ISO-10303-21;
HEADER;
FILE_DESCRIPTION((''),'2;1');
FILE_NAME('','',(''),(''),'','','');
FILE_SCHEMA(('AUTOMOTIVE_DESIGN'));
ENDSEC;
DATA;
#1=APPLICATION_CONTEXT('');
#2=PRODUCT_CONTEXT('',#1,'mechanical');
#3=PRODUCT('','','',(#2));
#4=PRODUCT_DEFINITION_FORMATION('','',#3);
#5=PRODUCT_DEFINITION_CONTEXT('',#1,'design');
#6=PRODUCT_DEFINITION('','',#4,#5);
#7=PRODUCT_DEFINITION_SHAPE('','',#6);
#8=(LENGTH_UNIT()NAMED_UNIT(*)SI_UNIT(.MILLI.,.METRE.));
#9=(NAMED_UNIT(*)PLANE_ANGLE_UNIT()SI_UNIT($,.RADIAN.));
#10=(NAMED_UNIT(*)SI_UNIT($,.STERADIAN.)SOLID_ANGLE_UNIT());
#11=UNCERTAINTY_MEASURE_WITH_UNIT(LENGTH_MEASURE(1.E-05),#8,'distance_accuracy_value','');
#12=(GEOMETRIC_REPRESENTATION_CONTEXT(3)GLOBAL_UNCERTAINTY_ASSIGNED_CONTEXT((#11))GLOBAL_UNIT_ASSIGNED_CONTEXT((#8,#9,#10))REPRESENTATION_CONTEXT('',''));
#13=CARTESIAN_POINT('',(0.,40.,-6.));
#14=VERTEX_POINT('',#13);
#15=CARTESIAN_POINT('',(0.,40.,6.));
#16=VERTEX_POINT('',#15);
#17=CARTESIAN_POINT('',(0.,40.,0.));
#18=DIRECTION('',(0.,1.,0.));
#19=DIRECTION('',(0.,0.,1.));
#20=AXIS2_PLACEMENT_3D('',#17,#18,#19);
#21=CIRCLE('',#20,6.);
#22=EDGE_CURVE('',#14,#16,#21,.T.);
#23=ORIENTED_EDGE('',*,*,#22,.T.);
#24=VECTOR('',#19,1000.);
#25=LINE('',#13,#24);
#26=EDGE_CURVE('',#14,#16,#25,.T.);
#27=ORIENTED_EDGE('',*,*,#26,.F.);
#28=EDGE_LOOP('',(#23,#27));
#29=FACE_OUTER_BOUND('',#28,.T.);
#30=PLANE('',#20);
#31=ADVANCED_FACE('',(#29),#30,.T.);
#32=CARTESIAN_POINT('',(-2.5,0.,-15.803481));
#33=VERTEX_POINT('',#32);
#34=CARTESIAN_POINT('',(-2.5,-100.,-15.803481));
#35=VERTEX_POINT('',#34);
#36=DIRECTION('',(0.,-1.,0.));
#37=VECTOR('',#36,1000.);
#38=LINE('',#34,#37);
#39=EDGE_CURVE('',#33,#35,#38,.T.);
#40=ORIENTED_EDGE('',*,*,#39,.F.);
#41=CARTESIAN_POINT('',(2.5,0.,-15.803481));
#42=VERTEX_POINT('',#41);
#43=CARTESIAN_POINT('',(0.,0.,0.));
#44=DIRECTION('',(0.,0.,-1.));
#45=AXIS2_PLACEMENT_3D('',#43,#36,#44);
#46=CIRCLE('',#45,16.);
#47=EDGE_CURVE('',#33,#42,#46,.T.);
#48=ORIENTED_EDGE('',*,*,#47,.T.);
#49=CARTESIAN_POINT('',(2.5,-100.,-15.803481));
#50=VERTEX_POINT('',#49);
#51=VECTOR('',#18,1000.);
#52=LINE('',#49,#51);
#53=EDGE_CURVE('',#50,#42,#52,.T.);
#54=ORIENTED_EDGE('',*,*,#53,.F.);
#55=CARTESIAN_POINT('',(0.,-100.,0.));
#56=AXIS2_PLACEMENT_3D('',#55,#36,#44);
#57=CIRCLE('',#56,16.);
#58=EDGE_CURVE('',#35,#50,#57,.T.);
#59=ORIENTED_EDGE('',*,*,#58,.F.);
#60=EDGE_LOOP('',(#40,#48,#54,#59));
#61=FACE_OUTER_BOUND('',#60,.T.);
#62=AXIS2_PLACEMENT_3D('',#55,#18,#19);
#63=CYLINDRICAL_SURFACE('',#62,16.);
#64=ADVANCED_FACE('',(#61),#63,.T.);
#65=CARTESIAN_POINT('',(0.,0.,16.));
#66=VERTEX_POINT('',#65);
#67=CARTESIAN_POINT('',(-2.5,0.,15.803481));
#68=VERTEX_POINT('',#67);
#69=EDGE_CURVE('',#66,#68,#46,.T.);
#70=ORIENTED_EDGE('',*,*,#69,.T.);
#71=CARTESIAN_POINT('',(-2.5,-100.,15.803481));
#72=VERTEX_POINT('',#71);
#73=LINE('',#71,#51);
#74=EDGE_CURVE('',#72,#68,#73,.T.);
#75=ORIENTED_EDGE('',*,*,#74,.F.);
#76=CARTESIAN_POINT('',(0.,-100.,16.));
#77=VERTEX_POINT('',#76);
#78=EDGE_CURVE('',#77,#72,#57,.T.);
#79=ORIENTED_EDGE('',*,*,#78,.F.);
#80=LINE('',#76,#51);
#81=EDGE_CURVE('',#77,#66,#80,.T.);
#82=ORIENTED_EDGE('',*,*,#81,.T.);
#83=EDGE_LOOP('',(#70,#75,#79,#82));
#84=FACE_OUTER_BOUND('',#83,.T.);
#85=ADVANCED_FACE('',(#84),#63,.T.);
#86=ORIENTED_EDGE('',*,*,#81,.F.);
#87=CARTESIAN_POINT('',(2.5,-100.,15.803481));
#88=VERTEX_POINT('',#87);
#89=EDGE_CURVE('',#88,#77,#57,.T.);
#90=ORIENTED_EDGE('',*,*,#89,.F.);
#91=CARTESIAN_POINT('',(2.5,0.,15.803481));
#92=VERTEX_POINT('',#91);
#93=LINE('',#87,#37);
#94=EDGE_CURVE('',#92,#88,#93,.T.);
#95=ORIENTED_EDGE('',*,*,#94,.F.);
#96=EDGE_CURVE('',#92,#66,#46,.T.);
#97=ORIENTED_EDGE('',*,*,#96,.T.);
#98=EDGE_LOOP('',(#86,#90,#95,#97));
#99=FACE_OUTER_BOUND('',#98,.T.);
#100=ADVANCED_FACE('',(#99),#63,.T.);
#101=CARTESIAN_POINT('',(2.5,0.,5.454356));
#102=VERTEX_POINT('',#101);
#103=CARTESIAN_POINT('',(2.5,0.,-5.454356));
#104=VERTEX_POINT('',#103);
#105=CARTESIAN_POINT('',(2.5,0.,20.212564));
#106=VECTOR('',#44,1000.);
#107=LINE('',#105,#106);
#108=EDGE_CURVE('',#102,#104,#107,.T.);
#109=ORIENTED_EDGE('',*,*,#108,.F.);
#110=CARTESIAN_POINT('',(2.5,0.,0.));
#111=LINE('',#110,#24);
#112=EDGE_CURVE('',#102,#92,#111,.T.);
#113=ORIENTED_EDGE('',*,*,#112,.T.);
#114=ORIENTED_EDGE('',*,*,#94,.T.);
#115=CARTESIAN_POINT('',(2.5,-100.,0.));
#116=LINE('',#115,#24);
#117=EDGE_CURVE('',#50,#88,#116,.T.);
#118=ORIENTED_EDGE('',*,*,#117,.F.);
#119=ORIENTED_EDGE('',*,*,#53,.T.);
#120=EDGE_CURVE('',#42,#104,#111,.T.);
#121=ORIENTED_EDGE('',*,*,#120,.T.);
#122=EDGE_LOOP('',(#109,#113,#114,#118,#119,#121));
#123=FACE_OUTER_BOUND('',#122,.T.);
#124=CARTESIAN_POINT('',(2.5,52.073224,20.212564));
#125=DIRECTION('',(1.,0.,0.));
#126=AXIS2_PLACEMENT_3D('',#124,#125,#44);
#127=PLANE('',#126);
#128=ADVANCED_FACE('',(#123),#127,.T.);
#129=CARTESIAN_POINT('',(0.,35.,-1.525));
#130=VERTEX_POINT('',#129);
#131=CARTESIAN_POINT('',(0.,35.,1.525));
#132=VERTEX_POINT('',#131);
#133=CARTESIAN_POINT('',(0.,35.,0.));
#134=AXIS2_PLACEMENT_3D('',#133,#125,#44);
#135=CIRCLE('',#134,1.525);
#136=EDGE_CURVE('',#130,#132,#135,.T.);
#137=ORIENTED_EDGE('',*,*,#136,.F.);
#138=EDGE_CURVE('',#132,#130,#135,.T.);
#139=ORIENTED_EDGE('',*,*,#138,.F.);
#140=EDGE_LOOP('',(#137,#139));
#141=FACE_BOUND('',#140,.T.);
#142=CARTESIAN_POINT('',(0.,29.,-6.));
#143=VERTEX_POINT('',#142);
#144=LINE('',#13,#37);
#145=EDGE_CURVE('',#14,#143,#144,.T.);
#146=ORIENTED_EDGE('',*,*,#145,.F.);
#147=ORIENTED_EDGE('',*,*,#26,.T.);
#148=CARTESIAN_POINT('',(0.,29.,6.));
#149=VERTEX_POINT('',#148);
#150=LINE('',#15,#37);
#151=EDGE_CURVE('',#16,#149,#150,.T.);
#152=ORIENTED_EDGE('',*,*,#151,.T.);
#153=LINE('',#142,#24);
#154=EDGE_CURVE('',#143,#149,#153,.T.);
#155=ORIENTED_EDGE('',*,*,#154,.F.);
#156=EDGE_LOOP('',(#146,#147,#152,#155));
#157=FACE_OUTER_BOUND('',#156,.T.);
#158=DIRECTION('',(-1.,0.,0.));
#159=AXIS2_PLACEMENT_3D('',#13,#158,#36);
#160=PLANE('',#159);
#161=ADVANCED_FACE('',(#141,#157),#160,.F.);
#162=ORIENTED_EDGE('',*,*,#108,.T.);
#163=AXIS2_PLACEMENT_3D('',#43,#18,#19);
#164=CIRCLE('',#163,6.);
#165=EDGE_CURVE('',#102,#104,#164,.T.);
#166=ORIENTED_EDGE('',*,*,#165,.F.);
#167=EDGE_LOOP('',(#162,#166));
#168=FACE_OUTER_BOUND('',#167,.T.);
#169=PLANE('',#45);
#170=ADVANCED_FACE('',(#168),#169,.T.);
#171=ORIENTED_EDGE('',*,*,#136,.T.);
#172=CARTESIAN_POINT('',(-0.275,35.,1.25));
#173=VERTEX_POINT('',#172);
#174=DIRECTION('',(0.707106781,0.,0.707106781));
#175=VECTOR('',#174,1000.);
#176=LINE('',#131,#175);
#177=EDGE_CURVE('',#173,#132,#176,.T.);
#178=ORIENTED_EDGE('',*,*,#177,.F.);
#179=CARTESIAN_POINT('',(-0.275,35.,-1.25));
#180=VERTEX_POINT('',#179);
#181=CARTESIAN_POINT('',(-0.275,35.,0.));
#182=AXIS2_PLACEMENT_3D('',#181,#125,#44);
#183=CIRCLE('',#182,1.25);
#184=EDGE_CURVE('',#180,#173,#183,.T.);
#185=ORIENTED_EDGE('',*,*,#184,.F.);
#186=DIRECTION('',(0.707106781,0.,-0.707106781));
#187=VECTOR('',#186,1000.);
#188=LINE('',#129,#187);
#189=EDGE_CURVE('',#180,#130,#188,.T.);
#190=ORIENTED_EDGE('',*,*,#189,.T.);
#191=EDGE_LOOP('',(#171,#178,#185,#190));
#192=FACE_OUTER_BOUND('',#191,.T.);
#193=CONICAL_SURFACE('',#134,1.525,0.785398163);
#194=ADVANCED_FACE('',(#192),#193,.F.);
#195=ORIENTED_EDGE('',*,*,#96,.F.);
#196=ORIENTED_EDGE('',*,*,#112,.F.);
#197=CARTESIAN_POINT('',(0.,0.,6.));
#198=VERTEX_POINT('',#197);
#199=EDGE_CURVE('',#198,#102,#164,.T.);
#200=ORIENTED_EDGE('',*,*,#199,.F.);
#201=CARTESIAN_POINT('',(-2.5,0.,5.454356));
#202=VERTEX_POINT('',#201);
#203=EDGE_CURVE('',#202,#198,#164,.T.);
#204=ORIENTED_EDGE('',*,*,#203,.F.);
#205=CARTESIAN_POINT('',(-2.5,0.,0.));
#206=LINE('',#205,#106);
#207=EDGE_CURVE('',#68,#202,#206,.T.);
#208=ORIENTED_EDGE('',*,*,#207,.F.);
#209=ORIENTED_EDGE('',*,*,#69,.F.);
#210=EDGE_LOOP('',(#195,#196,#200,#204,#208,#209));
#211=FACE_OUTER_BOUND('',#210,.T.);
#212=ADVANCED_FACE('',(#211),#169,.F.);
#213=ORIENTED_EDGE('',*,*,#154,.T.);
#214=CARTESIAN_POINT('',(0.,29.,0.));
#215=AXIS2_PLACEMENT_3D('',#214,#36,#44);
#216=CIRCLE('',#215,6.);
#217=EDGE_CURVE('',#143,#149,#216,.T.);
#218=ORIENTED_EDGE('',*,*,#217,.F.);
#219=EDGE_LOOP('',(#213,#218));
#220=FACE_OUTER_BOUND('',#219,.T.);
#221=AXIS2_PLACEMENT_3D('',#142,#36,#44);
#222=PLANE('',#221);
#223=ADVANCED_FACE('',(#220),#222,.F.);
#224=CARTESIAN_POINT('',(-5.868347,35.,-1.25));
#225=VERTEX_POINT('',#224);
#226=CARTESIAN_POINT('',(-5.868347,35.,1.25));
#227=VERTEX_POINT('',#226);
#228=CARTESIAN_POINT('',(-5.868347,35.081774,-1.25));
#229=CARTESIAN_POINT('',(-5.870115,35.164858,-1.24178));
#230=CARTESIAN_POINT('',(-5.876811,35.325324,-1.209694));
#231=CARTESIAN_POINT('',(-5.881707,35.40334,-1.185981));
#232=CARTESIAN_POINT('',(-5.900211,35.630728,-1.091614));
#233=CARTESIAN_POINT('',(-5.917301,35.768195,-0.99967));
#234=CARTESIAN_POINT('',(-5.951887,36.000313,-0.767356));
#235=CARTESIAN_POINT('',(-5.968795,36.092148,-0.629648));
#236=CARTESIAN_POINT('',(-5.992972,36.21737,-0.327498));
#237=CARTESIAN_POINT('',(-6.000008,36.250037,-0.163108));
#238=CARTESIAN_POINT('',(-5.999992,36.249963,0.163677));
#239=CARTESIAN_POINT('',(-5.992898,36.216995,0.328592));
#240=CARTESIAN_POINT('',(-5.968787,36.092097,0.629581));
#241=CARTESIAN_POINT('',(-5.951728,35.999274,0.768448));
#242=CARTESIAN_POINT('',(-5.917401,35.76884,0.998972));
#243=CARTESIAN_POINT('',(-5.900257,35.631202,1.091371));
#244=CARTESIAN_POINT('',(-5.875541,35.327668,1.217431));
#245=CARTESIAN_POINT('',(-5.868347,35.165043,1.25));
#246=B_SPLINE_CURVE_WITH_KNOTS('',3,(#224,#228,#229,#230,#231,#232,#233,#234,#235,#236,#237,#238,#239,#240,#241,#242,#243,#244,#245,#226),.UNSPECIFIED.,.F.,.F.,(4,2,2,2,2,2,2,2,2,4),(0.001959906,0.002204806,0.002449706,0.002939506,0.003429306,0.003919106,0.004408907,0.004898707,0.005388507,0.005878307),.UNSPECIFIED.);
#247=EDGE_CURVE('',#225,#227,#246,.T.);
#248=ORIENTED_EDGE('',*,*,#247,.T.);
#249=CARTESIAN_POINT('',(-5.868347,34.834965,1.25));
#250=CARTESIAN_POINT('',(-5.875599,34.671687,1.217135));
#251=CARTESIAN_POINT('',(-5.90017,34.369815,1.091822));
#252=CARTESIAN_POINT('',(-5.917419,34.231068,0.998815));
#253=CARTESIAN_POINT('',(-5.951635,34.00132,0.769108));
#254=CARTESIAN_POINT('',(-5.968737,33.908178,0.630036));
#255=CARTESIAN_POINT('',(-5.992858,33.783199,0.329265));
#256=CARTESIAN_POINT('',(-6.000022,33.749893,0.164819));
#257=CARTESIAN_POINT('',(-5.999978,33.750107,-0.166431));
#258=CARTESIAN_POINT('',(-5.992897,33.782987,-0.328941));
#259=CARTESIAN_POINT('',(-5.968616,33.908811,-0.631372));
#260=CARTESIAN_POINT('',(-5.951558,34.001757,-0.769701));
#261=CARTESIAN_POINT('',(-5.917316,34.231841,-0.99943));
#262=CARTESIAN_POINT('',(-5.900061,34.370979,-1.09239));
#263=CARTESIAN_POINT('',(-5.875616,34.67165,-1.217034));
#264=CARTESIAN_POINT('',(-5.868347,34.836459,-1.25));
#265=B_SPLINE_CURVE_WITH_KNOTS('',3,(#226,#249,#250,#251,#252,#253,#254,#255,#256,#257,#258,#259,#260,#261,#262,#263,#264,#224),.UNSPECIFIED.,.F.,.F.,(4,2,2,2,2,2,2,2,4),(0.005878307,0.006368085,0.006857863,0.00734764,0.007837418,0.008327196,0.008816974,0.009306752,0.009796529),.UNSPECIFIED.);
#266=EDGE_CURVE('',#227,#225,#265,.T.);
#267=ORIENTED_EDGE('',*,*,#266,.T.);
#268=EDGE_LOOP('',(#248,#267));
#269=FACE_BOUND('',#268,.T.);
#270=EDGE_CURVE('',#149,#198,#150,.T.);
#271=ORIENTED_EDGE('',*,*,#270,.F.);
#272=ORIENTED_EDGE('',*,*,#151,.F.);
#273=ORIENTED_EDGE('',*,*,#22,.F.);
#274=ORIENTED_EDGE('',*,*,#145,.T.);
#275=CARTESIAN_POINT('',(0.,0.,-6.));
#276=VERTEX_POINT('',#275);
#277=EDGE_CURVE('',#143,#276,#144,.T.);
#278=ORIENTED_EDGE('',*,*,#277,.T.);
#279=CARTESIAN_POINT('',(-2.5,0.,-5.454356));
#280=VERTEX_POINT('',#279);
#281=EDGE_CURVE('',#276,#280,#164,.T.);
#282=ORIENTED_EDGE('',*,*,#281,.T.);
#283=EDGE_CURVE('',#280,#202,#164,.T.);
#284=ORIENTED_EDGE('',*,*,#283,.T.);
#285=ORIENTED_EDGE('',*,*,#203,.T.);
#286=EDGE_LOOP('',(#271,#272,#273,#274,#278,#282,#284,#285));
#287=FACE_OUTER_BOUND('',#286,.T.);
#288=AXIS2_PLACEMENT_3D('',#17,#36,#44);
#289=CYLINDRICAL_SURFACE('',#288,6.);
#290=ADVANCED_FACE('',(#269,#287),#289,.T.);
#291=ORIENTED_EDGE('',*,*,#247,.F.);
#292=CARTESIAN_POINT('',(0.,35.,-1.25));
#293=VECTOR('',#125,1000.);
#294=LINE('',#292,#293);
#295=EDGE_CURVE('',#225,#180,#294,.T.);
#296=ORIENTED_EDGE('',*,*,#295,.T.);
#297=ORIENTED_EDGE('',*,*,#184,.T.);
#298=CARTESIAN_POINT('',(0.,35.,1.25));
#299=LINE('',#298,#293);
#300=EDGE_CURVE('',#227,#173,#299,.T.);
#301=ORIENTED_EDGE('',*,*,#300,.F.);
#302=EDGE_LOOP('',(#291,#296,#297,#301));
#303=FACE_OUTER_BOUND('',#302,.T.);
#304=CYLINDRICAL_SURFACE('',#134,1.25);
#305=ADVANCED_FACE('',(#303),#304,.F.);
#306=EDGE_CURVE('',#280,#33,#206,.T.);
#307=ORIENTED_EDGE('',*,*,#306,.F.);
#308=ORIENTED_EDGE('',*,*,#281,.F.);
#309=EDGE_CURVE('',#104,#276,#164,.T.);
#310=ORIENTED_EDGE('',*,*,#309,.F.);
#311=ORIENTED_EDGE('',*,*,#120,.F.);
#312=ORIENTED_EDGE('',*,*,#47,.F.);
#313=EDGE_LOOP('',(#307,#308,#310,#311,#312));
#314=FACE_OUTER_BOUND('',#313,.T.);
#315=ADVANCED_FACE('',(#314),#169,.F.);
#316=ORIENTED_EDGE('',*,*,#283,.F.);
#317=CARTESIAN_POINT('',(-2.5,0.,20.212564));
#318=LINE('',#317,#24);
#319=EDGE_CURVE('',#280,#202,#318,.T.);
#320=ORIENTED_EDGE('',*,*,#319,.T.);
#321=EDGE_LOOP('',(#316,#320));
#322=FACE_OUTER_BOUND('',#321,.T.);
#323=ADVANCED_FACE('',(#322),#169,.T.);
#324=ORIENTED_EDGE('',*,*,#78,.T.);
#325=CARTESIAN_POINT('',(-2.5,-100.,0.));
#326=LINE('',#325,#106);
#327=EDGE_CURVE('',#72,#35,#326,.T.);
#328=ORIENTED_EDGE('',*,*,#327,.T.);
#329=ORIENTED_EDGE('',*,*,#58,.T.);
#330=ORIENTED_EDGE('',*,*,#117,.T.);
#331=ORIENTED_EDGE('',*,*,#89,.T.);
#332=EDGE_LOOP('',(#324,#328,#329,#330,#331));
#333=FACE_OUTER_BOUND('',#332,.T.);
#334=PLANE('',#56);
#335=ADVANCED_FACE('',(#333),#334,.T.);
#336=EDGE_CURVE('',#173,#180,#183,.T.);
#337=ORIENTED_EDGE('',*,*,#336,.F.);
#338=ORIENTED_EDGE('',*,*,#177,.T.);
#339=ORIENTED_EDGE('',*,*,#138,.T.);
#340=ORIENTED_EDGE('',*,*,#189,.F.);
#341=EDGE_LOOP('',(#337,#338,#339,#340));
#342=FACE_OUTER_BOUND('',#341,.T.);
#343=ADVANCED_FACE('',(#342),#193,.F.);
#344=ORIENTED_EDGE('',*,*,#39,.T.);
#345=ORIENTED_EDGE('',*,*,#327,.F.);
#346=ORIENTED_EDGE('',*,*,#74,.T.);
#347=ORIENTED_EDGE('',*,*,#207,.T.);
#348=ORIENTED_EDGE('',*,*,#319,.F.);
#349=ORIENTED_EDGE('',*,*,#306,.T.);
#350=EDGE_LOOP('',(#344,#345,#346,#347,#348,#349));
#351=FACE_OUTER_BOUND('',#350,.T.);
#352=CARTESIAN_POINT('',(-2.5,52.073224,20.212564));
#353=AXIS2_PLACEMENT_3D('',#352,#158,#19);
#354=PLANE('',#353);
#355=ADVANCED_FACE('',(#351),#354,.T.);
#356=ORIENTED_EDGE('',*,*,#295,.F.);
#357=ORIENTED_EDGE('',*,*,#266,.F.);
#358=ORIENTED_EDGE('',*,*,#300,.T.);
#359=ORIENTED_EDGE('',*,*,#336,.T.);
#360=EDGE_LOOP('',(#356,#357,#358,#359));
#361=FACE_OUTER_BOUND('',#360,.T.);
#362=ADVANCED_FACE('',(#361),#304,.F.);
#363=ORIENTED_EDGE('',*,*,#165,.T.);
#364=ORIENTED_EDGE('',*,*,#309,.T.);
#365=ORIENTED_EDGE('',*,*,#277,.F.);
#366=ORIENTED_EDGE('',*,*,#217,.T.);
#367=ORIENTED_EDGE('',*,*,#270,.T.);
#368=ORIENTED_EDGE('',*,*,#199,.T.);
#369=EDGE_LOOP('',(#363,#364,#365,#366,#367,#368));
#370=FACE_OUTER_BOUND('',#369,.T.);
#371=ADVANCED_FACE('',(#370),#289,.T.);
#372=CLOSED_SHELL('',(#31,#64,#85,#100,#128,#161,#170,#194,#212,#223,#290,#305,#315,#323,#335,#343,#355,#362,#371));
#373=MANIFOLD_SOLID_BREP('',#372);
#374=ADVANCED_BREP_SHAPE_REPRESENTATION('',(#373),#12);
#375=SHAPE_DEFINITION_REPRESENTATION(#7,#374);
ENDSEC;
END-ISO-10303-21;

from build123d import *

# Parameters (mm, degrees)
SKETCH1_R                   = 6
BOSS_EXTRUDE1_DEPTH         = 40
CUT_EXTRUDE1_DEPTH          = 41.890096601
CUT_EXTRUDE1_DEPTH_BACK     = 41.890096601
SKETCH2_W                   = 18.470240229
SKETCH2_H                   = 11
M3_TAPPED_HOLE2_D           = 2.5
M3_TAPPED_HOLE2_CSINK_D     = 3.05
M3_TAPPED_HOLE2_CSINK_ANGLE = 90
SKETCH5_R                   = 16
BOSS_EXTRUDE2_DEPTH         = 100
CUT_EXTRUDE2_DEPTH          = 142.816783309
CUT_EXTRUDE2_DEPTH_BACK     = 100
SKETCH11_OUTSIDE_W          = 63.426
SKETCH11_OUTSIDE_H          = 63.426
SKETCH11_OUTSIDE_W_2        = 5
SKETCH11_OUTSIDE_H_2        = 40.425128238


with BuildPart() as part:
    # Sketch1 → Boss-Extrude1 (new body)
    with BuildSketch(Plane(origin=(0, 0, 0), x_dir=(1, 0, 0), z_dir=(0, 1, 0))):
        with Locations(Location((0, 0, 0), (0, 0, 270))):
            Circle(SKETCH1_R)
    extrude(amount=BOSS_EXTRUDE1_DEPTH)

    # Sketch2 → Cut-Extrude1 (cut, two sides: drawn at the far end of the back side and taken through both)
    with BuildSketch(Plane.XY.offset(-CUT_EXTRUDE1_DEPTH_BACK)):
        with Locations((9.235120115, 34.5)):
            Rectangle(SKETCH2_W, SKETCH2_H)
    extrude(amount=CUT_EXTRUDE1_DEPTH + CUT_EXTRUDE1_DEPTH_BACK, mode=Mode.SUBTRACT)

    # M3 Tapped Hole2 (through all)
    with Locations(Plane(origin=(0, 0, 0), x_dir=(0, 0, -1), z_dir=(1, 0, 0))):
        with Locations((0, 35)):
            CounterSinkHole(M3_TAPPED_HOLE2_D / 2, M3_TAPPED_HOLE2_CSINK_D / 2, counter_sink_angle=M3_TAPPED_HOLE2_CSINK_ANGLE)

    # Sketch5 → Boss-Extrude2 (add)
    with BuildSketch(Plane.XZ):
        with Locations(Location((0, 0, 0), (0, 0, 270))):
            Circle(SKETCH5_R)
    extrude(amount=BOSS_EXTRUDE2_DEPTH)

    # Sketch11 outside → Cut-Extrude2 (cut, two sides: drawn at the far end of the back side and taken through both)
    with BuildSketch(Plane.XZ.offset(100).offset(-CUT_EXTRUDE2_DEPTH_BACK)):
        Rectangle(SKETCH11_OUTSIDE_W, SKETCH11_OUTSIDE_H)
        Rectangle(SKETCH11_OUTSIDE_W_2, SKETCH11_OUTSIDE_H_2, mode=Mode.SUBTRACT)
    extrude(amount=CUT_EXTRUDE2_DEPTH + CUT_EXTRUDE2_DEPTH_BACK, mode=Mode.SUBTRACT)


solid = part.part
